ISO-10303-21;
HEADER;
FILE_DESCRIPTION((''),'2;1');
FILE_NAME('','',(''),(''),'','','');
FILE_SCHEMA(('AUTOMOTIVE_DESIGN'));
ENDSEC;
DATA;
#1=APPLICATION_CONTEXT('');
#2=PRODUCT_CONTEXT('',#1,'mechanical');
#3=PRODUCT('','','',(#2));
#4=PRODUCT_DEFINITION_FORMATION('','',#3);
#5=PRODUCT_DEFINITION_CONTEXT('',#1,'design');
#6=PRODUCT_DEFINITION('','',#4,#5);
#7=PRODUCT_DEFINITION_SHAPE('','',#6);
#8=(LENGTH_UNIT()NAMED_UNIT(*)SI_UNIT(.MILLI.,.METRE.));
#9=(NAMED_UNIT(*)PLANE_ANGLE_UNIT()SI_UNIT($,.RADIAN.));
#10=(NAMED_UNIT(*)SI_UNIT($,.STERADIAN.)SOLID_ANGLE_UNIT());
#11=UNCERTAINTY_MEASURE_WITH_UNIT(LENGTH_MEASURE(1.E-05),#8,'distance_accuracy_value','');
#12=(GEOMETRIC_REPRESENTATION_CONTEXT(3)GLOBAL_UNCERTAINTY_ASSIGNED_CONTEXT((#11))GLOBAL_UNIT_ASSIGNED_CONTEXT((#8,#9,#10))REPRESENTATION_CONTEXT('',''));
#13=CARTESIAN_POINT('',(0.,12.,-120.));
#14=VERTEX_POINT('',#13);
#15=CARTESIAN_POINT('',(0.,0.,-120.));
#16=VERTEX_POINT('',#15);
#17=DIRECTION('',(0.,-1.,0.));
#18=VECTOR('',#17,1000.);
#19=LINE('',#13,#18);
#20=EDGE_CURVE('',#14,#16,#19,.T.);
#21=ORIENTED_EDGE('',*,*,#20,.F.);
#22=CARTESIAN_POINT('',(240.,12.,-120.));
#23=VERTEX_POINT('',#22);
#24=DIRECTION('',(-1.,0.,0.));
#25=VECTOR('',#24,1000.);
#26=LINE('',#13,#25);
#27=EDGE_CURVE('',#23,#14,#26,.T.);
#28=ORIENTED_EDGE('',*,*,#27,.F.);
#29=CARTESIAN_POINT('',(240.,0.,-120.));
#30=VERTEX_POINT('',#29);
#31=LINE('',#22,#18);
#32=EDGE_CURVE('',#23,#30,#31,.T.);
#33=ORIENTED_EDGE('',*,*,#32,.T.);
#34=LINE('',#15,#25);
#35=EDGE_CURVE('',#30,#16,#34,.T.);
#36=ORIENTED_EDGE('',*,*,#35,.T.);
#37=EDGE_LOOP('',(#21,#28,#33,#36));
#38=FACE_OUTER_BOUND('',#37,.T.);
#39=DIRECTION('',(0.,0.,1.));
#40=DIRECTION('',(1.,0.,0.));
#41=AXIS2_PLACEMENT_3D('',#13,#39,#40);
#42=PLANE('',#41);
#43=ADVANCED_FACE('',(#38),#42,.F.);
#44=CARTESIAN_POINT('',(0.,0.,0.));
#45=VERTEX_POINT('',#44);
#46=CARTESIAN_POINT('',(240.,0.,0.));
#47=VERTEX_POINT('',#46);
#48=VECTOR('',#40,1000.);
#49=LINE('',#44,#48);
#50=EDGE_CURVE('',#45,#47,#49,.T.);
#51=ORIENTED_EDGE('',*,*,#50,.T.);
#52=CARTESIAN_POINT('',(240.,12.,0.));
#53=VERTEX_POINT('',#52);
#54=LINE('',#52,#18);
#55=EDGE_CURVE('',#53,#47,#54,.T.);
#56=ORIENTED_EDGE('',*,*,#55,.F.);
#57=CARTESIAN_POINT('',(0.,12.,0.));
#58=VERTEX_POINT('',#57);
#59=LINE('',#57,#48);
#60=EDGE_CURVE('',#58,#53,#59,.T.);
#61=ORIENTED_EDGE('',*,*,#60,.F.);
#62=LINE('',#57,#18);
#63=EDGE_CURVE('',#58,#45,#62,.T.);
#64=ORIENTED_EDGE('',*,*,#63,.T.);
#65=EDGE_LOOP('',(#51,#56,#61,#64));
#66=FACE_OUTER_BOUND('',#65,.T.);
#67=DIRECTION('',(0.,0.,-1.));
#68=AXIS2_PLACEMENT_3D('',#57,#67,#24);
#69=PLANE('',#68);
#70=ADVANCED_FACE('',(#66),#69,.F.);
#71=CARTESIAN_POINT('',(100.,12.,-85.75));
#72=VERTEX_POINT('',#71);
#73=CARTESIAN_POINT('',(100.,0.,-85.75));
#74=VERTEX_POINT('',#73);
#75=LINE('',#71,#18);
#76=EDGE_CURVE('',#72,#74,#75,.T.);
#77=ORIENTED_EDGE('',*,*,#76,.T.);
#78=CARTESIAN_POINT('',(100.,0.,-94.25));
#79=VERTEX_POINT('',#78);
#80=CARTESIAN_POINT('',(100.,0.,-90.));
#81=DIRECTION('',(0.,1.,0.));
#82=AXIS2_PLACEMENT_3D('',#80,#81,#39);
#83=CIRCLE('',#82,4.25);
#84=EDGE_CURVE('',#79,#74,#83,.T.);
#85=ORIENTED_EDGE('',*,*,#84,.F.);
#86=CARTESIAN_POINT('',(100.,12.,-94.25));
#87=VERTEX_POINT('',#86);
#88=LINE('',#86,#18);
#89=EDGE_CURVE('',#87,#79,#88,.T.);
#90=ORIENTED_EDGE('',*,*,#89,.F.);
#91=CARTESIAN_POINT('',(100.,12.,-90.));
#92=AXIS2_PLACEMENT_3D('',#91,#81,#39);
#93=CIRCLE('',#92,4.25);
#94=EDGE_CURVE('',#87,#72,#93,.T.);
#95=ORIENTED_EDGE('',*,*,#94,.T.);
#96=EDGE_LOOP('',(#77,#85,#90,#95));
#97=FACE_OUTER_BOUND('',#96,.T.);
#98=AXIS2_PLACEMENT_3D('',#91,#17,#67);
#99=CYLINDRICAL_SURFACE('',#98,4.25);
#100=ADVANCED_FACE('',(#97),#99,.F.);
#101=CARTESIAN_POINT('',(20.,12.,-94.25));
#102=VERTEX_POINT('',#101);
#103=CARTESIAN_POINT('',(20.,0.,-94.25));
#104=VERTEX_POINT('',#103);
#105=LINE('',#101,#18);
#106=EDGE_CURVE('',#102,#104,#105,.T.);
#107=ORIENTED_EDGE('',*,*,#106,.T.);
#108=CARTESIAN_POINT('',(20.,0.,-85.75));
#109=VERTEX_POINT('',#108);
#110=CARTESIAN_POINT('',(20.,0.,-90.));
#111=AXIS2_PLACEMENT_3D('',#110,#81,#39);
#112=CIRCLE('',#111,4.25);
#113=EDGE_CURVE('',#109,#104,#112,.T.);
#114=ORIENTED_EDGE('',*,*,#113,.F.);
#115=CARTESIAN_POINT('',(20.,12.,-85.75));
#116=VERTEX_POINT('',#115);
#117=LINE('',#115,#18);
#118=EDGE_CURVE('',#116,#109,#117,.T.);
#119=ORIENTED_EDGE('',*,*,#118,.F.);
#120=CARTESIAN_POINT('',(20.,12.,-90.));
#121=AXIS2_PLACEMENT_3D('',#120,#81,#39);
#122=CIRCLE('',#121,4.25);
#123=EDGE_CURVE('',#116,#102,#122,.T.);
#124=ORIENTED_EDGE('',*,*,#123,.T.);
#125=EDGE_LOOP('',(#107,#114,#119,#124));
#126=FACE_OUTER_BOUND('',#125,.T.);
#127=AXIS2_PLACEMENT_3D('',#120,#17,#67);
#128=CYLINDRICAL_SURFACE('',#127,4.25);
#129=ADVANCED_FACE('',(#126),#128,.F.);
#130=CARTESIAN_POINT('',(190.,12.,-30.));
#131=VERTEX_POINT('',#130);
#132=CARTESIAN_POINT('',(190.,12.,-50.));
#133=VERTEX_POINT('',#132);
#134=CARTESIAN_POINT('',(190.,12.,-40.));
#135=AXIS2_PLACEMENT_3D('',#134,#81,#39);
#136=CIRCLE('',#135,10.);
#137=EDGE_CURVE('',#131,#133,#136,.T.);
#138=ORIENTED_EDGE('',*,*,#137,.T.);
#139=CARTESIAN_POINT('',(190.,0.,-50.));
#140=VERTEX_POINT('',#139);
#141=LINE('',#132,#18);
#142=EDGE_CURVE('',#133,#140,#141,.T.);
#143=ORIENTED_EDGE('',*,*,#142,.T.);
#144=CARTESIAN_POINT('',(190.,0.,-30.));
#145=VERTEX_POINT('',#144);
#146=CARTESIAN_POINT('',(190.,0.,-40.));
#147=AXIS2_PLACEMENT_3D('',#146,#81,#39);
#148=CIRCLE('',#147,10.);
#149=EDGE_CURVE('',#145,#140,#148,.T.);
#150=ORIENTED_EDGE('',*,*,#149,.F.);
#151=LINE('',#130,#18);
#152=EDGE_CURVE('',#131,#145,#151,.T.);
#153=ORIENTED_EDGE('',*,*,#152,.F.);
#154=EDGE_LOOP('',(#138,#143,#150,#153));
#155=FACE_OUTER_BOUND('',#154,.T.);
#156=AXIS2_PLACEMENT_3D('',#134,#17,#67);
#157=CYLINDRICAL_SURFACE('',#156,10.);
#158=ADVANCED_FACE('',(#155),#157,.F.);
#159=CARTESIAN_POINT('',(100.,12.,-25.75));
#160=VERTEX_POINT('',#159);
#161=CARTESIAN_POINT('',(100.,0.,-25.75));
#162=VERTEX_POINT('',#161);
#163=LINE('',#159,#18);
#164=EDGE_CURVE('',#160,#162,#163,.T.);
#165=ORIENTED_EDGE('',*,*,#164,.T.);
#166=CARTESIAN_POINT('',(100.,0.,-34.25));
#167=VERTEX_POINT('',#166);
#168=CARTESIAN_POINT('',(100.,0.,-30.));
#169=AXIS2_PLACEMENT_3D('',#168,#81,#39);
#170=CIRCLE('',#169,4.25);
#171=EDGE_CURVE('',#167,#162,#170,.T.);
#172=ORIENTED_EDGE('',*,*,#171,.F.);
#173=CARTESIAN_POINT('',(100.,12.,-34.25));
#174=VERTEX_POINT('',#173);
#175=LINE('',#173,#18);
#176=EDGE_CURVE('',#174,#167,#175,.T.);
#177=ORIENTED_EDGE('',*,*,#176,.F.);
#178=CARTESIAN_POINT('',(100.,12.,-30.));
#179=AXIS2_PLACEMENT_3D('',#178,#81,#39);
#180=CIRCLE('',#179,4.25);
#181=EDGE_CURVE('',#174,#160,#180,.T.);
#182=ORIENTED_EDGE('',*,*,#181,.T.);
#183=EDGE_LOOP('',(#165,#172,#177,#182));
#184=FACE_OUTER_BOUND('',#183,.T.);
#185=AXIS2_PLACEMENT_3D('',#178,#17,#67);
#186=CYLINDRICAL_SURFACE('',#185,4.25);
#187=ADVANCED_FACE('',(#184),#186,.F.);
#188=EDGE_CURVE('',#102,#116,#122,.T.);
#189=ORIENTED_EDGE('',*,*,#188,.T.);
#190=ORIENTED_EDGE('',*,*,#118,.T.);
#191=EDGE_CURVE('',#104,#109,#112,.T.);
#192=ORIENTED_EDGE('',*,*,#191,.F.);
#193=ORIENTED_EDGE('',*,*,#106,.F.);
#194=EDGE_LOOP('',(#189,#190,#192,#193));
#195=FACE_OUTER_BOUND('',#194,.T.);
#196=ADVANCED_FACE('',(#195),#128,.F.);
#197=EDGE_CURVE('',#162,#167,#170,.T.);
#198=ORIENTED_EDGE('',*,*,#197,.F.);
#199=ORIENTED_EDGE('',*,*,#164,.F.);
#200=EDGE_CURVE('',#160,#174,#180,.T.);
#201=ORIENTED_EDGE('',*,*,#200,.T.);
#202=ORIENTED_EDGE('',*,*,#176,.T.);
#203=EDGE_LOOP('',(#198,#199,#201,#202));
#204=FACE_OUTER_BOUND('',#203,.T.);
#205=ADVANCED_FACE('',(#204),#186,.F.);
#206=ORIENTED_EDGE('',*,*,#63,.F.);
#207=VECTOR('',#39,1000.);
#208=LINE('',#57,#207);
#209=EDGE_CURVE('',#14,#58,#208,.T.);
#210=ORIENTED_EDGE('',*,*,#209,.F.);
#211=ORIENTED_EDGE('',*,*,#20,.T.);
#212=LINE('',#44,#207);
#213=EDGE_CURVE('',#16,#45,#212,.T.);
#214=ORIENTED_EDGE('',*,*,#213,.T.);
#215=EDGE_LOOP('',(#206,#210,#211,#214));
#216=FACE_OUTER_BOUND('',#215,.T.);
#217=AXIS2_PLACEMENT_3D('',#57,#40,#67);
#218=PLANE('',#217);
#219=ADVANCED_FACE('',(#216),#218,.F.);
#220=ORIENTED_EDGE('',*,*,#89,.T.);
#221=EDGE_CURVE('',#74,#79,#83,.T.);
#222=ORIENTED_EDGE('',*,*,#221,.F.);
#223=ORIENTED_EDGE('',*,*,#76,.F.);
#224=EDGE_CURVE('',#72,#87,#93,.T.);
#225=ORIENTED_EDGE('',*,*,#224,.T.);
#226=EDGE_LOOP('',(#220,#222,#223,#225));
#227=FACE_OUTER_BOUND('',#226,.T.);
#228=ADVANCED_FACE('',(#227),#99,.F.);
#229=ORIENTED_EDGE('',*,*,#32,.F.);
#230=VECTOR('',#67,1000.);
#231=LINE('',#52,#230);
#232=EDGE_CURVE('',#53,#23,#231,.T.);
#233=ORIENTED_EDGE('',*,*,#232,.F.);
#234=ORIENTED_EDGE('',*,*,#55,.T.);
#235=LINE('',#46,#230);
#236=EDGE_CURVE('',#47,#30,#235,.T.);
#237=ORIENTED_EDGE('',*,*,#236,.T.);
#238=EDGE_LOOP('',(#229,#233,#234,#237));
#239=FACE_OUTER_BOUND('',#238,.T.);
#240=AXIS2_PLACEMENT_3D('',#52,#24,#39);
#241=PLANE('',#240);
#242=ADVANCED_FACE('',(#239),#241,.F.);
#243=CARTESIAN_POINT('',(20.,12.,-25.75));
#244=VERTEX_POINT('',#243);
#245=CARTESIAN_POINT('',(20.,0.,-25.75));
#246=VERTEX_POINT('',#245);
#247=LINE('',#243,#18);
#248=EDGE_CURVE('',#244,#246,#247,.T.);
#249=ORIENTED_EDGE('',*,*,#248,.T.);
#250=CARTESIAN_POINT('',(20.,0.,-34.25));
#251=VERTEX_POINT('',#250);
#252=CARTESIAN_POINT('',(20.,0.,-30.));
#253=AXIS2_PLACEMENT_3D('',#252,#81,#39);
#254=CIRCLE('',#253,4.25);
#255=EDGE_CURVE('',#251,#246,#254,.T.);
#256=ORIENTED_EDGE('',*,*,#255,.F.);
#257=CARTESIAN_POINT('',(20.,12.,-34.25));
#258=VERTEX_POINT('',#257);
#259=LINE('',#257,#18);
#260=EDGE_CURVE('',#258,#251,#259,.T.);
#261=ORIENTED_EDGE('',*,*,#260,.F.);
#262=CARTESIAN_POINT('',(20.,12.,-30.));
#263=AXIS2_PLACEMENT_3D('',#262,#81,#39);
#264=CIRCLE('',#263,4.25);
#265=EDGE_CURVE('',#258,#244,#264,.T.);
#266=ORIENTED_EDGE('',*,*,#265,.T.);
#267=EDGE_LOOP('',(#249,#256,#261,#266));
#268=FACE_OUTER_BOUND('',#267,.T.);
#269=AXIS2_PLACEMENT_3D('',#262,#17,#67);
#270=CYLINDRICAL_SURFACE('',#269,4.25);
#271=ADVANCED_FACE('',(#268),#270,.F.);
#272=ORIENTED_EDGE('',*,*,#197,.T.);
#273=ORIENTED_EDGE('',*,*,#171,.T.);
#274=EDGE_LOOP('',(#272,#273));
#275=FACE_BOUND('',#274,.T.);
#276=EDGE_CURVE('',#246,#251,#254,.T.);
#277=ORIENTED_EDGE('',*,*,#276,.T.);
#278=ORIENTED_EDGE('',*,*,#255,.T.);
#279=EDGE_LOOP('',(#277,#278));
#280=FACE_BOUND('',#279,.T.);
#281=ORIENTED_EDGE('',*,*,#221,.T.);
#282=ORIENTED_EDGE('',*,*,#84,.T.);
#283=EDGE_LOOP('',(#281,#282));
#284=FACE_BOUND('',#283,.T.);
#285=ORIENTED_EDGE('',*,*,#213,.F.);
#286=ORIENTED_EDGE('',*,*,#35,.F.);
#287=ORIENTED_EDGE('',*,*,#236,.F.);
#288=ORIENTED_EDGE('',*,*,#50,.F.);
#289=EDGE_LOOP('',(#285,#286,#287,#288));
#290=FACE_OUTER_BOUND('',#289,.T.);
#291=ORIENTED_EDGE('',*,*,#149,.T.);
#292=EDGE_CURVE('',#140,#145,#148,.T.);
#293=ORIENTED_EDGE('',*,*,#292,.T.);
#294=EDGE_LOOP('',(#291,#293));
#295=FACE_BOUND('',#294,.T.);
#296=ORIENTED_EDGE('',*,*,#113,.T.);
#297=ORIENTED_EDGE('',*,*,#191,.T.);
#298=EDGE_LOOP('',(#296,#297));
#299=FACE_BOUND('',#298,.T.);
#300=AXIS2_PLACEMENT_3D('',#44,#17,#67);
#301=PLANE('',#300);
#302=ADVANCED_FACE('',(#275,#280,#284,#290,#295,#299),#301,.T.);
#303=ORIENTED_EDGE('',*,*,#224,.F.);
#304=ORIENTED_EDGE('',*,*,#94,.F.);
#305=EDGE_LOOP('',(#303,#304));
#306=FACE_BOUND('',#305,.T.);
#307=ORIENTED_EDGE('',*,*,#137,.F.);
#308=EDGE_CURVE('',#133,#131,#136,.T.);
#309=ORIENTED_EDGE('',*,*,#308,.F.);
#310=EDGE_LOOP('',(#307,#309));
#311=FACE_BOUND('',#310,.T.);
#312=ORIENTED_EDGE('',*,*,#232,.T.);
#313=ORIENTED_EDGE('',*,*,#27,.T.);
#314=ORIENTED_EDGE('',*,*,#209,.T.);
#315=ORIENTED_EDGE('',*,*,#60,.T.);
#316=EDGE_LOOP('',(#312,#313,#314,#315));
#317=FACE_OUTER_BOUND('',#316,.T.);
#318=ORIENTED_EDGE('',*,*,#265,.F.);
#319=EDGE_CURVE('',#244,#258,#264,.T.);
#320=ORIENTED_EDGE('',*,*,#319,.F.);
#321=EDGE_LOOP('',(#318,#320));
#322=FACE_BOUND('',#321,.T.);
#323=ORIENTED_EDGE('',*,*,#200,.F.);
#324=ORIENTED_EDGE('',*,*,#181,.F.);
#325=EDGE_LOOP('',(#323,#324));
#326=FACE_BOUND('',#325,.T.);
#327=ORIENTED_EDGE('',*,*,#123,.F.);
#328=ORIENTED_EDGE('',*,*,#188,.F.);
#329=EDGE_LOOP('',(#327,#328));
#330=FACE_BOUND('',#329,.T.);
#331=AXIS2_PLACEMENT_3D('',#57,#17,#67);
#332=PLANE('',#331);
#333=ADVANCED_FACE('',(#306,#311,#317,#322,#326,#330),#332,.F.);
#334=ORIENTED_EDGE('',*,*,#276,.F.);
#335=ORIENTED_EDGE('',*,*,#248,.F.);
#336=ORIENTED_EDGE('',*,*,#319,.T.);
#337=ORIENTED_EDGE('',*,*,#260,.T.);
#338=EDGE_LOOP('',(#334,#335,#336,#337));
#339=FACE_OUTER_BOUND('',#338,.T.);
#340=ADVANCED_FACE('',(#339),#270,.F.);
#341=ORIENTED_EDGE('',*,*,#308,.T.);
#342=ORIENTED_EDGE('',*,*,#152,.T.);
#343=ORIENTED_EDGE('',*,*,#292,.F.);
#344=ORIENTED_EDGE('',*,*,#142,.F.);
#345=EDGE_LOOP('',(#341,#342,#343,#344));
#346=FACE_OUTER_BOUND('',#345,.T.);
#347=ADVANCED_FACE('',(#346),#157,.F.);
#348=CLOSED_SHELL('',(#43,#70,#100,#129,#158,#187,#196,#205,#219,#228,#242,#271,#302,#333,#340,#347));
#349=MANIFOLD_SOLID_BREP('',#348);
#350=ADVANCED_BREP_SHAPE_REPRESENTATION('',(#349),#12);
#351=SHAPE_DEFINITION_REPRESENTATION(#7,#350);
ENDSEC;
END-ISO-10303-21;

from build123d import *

# Parameters (mm, degrees)
SKETCH_1_W      = 240
SKETCH_1_H      = 120
SKETCH_1_R      = 4.25
SKETCH_1_R_2    = 10
EXTRUDE_1_DEPTH = 12


with BuildPart() as part:
    # 草图1 → 凸台-拉伸1 (new body)
    with BuildSketch(Plane(origin=(0, 0, 0), x_dir=(1, 0, 0), z_dir=(0, 1, 0))):
        with Locations((120, 60)):
            Rectangle(SKETCH_1_W, SKETCH_1_H)
        with Locations(Location((20, 30, 0), (0, 0, 270))):
            Circle(SKETCH_1_R, mode=Mode.SUBTRACT)
        with Locations(Location((20, 90, 0), (0, 0, 270))):
            Circle(SKETCH_1_R, mode=Mode.SUBTRACT)
        with Locations(Location((100, 90, 0), (0, 0, 270))):
            Circle(SKETCH_1_R, mode=Mode.SUBTRACT)
        with Locations(Location((100, 30, 0), (0, 0, 270))):
            Circle(SKETCH_1_R, mode=Mode.SUBTRACT)
        with Locations(Location((190, 40, 0), (0, 0, 270))):
            Circle(SKETCH_1_R_2, mode=Mode.SUBTRACT)
    extrude(amount=EXTRUDE_1_DEPTH)


solid = part.part
